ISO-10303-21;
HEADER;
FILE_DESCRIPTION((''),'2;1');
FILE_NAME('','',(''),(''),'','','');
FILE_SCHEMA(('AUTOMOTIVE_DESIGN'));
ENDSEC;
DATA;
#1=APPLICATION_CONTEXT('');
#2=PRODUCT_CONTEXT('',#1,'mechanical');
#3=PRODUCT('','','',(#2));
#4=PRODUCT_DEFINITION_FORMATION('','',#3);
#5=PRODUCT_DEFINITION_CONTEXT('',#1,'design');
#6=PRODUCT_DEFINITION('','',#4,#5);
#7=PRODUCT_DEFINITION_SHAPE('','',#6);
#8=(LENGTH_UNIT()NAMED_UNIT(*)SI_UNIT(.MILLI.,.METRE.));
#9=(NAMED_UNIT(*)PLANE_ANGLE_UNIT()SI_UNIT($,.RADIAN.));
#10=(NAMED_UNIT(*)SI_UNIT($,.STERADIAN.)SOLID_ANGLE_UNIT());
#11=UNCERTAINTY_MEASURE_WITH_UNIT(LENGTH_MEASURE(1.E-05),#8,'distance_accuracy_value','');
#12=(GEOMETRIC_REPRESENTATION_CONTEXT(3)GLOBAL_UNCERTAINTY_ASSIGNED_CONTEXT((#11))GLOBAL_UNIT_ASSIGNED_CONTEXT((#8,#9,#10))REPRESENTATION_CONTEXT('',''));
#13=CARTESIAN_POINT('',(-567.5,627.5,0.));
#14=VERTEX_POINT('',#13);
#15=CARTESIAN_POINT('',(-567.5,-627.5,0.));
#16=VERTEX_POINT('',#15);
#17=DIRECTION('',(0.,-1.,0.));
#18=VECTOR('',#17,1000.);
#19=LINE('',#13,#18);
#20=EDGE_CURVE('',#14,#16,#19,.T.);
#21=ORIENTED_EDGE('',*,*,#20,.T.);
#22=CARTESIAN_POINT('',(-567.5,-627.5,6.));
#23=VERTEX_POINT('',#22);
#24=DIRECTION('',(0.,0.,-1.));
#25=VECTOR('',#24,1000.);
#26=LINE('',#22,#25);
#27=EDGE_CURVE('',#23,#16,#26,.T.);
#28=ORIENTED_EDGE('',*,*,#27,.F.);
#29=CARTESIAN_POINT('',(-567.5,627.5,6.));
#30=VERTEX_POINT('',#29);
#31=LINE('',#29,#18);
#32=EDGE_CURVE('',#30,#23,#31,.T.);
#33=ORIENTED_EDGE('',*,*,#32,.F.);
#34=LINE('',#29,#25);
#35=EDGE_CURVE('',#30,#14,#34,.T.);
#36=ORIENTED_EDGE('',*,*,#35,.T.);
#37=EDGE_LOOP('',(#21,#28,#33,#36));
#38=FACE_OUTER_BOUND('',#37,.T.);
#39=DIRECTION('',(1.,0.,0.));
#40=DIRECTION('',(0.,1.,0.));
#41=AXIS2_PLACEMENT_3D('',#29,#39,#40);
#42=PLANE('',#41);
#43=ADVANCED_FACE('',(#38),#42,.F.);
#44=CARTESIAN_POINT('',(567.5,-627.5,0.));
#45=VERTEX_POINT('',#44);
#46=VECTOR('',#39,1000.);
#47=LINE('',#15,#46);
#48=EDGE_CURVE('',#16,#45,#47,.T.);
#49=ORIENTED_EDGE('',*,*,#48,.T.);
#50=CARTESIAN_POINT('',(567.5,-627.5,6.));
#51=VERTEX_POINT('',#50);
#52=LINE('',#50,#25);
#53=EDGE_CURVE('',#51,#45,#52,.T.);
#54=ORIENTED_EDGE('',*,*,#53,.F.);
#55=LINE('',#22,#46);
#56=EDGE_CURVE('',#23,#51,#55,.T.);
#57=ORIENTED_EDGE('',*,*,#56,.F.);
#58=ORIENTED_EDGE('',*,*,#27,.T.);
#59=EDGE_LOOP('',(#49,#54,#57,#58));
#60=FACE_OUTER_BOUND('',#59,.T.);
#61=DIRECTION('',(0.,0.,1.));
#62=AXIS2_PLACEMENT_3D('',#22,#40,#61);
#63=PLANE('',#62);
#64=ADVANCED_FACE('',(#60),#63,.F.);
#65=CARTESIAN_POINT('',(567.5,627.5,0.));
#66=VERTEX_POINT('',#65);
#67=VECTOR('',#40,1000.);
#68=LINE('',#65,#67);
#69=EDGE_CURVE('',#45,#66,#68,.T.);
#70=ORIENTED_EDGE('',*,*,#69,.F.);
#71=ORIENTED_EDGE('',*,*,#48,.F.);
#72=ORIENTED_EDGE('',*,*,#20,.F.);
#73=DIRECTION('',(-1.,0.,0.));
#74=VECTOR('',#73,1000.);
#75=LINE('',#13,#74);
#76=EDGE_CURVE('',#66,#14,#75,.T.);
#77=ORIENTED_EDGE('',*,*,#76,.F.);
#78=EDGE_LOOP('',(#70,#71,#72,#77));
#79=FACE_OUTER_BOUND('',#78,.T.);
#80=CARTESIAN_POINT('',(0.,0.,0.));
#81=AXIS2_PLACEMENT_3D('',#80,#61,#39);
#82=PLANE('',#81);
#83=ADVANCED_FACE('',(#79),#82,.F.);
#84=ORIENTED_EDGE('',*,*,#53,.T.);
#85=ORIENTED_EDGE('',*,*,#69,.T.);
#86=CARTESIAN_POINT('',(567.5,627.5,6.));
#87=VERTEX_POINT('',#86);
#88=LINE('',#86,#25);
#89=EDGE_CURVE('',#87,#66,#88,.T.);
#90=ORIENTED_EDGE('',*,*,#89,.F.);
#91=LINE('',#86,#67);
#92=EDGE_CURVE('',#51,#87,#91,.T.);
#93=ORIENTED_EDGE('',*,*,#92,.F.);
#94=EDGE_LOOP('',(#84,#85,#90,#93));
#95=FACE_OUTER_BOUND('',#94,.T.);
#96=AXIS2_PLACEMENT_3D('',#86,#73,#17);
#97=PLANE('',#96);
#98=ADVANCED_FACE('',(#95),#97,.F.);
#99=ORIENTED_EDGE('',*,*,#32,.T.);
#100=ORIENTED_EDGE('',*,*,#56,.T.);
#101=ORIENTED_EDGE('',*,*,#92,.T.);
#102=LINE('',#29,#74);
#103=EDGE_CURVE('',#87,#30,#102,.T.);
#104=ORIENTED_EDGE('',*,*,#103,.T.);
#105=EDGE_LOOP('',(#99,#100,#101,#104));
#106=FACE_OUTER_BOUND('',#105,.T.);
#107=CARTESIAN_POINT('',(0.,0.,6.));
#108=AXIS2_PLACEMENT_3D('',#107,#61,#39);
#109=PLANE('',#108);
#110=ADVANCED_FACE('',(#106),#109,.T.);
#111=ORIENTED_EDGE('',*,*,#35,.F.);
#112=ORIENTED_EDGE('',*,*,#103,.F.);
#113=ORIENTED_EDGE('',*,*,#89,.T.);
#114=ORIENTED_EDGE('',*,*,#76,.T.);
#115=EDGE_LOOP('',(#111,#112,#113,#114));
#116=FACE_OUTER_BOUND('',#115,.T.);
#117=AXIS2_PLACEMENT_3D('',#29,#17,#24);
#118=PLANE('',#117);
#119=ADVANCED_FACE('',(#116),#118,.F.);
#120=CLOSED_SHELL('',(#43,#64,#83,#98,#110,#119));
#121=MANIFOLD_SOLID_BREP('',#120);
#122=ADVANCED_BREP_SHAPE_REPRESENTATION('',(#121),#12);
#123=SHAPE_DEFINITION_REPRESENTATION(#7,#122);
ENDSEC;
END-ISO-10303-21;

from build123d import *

# Parameters (mm, degrees)
SKETCH_1_W      = 1135
SKETCH_1_H      = 1255
EXTRUDE_1_DEPTH = 6


with BuildPart() as part:
    # 草图1 → 凸台-拉伸1 (new body)
    with BuildSketch(Plane.XY):
        Rectangle(SKETCH_1_W, SKETCH_1_H)
    extrude(amount=EXTRUDE_1_DEPTH)


solid = part.part
